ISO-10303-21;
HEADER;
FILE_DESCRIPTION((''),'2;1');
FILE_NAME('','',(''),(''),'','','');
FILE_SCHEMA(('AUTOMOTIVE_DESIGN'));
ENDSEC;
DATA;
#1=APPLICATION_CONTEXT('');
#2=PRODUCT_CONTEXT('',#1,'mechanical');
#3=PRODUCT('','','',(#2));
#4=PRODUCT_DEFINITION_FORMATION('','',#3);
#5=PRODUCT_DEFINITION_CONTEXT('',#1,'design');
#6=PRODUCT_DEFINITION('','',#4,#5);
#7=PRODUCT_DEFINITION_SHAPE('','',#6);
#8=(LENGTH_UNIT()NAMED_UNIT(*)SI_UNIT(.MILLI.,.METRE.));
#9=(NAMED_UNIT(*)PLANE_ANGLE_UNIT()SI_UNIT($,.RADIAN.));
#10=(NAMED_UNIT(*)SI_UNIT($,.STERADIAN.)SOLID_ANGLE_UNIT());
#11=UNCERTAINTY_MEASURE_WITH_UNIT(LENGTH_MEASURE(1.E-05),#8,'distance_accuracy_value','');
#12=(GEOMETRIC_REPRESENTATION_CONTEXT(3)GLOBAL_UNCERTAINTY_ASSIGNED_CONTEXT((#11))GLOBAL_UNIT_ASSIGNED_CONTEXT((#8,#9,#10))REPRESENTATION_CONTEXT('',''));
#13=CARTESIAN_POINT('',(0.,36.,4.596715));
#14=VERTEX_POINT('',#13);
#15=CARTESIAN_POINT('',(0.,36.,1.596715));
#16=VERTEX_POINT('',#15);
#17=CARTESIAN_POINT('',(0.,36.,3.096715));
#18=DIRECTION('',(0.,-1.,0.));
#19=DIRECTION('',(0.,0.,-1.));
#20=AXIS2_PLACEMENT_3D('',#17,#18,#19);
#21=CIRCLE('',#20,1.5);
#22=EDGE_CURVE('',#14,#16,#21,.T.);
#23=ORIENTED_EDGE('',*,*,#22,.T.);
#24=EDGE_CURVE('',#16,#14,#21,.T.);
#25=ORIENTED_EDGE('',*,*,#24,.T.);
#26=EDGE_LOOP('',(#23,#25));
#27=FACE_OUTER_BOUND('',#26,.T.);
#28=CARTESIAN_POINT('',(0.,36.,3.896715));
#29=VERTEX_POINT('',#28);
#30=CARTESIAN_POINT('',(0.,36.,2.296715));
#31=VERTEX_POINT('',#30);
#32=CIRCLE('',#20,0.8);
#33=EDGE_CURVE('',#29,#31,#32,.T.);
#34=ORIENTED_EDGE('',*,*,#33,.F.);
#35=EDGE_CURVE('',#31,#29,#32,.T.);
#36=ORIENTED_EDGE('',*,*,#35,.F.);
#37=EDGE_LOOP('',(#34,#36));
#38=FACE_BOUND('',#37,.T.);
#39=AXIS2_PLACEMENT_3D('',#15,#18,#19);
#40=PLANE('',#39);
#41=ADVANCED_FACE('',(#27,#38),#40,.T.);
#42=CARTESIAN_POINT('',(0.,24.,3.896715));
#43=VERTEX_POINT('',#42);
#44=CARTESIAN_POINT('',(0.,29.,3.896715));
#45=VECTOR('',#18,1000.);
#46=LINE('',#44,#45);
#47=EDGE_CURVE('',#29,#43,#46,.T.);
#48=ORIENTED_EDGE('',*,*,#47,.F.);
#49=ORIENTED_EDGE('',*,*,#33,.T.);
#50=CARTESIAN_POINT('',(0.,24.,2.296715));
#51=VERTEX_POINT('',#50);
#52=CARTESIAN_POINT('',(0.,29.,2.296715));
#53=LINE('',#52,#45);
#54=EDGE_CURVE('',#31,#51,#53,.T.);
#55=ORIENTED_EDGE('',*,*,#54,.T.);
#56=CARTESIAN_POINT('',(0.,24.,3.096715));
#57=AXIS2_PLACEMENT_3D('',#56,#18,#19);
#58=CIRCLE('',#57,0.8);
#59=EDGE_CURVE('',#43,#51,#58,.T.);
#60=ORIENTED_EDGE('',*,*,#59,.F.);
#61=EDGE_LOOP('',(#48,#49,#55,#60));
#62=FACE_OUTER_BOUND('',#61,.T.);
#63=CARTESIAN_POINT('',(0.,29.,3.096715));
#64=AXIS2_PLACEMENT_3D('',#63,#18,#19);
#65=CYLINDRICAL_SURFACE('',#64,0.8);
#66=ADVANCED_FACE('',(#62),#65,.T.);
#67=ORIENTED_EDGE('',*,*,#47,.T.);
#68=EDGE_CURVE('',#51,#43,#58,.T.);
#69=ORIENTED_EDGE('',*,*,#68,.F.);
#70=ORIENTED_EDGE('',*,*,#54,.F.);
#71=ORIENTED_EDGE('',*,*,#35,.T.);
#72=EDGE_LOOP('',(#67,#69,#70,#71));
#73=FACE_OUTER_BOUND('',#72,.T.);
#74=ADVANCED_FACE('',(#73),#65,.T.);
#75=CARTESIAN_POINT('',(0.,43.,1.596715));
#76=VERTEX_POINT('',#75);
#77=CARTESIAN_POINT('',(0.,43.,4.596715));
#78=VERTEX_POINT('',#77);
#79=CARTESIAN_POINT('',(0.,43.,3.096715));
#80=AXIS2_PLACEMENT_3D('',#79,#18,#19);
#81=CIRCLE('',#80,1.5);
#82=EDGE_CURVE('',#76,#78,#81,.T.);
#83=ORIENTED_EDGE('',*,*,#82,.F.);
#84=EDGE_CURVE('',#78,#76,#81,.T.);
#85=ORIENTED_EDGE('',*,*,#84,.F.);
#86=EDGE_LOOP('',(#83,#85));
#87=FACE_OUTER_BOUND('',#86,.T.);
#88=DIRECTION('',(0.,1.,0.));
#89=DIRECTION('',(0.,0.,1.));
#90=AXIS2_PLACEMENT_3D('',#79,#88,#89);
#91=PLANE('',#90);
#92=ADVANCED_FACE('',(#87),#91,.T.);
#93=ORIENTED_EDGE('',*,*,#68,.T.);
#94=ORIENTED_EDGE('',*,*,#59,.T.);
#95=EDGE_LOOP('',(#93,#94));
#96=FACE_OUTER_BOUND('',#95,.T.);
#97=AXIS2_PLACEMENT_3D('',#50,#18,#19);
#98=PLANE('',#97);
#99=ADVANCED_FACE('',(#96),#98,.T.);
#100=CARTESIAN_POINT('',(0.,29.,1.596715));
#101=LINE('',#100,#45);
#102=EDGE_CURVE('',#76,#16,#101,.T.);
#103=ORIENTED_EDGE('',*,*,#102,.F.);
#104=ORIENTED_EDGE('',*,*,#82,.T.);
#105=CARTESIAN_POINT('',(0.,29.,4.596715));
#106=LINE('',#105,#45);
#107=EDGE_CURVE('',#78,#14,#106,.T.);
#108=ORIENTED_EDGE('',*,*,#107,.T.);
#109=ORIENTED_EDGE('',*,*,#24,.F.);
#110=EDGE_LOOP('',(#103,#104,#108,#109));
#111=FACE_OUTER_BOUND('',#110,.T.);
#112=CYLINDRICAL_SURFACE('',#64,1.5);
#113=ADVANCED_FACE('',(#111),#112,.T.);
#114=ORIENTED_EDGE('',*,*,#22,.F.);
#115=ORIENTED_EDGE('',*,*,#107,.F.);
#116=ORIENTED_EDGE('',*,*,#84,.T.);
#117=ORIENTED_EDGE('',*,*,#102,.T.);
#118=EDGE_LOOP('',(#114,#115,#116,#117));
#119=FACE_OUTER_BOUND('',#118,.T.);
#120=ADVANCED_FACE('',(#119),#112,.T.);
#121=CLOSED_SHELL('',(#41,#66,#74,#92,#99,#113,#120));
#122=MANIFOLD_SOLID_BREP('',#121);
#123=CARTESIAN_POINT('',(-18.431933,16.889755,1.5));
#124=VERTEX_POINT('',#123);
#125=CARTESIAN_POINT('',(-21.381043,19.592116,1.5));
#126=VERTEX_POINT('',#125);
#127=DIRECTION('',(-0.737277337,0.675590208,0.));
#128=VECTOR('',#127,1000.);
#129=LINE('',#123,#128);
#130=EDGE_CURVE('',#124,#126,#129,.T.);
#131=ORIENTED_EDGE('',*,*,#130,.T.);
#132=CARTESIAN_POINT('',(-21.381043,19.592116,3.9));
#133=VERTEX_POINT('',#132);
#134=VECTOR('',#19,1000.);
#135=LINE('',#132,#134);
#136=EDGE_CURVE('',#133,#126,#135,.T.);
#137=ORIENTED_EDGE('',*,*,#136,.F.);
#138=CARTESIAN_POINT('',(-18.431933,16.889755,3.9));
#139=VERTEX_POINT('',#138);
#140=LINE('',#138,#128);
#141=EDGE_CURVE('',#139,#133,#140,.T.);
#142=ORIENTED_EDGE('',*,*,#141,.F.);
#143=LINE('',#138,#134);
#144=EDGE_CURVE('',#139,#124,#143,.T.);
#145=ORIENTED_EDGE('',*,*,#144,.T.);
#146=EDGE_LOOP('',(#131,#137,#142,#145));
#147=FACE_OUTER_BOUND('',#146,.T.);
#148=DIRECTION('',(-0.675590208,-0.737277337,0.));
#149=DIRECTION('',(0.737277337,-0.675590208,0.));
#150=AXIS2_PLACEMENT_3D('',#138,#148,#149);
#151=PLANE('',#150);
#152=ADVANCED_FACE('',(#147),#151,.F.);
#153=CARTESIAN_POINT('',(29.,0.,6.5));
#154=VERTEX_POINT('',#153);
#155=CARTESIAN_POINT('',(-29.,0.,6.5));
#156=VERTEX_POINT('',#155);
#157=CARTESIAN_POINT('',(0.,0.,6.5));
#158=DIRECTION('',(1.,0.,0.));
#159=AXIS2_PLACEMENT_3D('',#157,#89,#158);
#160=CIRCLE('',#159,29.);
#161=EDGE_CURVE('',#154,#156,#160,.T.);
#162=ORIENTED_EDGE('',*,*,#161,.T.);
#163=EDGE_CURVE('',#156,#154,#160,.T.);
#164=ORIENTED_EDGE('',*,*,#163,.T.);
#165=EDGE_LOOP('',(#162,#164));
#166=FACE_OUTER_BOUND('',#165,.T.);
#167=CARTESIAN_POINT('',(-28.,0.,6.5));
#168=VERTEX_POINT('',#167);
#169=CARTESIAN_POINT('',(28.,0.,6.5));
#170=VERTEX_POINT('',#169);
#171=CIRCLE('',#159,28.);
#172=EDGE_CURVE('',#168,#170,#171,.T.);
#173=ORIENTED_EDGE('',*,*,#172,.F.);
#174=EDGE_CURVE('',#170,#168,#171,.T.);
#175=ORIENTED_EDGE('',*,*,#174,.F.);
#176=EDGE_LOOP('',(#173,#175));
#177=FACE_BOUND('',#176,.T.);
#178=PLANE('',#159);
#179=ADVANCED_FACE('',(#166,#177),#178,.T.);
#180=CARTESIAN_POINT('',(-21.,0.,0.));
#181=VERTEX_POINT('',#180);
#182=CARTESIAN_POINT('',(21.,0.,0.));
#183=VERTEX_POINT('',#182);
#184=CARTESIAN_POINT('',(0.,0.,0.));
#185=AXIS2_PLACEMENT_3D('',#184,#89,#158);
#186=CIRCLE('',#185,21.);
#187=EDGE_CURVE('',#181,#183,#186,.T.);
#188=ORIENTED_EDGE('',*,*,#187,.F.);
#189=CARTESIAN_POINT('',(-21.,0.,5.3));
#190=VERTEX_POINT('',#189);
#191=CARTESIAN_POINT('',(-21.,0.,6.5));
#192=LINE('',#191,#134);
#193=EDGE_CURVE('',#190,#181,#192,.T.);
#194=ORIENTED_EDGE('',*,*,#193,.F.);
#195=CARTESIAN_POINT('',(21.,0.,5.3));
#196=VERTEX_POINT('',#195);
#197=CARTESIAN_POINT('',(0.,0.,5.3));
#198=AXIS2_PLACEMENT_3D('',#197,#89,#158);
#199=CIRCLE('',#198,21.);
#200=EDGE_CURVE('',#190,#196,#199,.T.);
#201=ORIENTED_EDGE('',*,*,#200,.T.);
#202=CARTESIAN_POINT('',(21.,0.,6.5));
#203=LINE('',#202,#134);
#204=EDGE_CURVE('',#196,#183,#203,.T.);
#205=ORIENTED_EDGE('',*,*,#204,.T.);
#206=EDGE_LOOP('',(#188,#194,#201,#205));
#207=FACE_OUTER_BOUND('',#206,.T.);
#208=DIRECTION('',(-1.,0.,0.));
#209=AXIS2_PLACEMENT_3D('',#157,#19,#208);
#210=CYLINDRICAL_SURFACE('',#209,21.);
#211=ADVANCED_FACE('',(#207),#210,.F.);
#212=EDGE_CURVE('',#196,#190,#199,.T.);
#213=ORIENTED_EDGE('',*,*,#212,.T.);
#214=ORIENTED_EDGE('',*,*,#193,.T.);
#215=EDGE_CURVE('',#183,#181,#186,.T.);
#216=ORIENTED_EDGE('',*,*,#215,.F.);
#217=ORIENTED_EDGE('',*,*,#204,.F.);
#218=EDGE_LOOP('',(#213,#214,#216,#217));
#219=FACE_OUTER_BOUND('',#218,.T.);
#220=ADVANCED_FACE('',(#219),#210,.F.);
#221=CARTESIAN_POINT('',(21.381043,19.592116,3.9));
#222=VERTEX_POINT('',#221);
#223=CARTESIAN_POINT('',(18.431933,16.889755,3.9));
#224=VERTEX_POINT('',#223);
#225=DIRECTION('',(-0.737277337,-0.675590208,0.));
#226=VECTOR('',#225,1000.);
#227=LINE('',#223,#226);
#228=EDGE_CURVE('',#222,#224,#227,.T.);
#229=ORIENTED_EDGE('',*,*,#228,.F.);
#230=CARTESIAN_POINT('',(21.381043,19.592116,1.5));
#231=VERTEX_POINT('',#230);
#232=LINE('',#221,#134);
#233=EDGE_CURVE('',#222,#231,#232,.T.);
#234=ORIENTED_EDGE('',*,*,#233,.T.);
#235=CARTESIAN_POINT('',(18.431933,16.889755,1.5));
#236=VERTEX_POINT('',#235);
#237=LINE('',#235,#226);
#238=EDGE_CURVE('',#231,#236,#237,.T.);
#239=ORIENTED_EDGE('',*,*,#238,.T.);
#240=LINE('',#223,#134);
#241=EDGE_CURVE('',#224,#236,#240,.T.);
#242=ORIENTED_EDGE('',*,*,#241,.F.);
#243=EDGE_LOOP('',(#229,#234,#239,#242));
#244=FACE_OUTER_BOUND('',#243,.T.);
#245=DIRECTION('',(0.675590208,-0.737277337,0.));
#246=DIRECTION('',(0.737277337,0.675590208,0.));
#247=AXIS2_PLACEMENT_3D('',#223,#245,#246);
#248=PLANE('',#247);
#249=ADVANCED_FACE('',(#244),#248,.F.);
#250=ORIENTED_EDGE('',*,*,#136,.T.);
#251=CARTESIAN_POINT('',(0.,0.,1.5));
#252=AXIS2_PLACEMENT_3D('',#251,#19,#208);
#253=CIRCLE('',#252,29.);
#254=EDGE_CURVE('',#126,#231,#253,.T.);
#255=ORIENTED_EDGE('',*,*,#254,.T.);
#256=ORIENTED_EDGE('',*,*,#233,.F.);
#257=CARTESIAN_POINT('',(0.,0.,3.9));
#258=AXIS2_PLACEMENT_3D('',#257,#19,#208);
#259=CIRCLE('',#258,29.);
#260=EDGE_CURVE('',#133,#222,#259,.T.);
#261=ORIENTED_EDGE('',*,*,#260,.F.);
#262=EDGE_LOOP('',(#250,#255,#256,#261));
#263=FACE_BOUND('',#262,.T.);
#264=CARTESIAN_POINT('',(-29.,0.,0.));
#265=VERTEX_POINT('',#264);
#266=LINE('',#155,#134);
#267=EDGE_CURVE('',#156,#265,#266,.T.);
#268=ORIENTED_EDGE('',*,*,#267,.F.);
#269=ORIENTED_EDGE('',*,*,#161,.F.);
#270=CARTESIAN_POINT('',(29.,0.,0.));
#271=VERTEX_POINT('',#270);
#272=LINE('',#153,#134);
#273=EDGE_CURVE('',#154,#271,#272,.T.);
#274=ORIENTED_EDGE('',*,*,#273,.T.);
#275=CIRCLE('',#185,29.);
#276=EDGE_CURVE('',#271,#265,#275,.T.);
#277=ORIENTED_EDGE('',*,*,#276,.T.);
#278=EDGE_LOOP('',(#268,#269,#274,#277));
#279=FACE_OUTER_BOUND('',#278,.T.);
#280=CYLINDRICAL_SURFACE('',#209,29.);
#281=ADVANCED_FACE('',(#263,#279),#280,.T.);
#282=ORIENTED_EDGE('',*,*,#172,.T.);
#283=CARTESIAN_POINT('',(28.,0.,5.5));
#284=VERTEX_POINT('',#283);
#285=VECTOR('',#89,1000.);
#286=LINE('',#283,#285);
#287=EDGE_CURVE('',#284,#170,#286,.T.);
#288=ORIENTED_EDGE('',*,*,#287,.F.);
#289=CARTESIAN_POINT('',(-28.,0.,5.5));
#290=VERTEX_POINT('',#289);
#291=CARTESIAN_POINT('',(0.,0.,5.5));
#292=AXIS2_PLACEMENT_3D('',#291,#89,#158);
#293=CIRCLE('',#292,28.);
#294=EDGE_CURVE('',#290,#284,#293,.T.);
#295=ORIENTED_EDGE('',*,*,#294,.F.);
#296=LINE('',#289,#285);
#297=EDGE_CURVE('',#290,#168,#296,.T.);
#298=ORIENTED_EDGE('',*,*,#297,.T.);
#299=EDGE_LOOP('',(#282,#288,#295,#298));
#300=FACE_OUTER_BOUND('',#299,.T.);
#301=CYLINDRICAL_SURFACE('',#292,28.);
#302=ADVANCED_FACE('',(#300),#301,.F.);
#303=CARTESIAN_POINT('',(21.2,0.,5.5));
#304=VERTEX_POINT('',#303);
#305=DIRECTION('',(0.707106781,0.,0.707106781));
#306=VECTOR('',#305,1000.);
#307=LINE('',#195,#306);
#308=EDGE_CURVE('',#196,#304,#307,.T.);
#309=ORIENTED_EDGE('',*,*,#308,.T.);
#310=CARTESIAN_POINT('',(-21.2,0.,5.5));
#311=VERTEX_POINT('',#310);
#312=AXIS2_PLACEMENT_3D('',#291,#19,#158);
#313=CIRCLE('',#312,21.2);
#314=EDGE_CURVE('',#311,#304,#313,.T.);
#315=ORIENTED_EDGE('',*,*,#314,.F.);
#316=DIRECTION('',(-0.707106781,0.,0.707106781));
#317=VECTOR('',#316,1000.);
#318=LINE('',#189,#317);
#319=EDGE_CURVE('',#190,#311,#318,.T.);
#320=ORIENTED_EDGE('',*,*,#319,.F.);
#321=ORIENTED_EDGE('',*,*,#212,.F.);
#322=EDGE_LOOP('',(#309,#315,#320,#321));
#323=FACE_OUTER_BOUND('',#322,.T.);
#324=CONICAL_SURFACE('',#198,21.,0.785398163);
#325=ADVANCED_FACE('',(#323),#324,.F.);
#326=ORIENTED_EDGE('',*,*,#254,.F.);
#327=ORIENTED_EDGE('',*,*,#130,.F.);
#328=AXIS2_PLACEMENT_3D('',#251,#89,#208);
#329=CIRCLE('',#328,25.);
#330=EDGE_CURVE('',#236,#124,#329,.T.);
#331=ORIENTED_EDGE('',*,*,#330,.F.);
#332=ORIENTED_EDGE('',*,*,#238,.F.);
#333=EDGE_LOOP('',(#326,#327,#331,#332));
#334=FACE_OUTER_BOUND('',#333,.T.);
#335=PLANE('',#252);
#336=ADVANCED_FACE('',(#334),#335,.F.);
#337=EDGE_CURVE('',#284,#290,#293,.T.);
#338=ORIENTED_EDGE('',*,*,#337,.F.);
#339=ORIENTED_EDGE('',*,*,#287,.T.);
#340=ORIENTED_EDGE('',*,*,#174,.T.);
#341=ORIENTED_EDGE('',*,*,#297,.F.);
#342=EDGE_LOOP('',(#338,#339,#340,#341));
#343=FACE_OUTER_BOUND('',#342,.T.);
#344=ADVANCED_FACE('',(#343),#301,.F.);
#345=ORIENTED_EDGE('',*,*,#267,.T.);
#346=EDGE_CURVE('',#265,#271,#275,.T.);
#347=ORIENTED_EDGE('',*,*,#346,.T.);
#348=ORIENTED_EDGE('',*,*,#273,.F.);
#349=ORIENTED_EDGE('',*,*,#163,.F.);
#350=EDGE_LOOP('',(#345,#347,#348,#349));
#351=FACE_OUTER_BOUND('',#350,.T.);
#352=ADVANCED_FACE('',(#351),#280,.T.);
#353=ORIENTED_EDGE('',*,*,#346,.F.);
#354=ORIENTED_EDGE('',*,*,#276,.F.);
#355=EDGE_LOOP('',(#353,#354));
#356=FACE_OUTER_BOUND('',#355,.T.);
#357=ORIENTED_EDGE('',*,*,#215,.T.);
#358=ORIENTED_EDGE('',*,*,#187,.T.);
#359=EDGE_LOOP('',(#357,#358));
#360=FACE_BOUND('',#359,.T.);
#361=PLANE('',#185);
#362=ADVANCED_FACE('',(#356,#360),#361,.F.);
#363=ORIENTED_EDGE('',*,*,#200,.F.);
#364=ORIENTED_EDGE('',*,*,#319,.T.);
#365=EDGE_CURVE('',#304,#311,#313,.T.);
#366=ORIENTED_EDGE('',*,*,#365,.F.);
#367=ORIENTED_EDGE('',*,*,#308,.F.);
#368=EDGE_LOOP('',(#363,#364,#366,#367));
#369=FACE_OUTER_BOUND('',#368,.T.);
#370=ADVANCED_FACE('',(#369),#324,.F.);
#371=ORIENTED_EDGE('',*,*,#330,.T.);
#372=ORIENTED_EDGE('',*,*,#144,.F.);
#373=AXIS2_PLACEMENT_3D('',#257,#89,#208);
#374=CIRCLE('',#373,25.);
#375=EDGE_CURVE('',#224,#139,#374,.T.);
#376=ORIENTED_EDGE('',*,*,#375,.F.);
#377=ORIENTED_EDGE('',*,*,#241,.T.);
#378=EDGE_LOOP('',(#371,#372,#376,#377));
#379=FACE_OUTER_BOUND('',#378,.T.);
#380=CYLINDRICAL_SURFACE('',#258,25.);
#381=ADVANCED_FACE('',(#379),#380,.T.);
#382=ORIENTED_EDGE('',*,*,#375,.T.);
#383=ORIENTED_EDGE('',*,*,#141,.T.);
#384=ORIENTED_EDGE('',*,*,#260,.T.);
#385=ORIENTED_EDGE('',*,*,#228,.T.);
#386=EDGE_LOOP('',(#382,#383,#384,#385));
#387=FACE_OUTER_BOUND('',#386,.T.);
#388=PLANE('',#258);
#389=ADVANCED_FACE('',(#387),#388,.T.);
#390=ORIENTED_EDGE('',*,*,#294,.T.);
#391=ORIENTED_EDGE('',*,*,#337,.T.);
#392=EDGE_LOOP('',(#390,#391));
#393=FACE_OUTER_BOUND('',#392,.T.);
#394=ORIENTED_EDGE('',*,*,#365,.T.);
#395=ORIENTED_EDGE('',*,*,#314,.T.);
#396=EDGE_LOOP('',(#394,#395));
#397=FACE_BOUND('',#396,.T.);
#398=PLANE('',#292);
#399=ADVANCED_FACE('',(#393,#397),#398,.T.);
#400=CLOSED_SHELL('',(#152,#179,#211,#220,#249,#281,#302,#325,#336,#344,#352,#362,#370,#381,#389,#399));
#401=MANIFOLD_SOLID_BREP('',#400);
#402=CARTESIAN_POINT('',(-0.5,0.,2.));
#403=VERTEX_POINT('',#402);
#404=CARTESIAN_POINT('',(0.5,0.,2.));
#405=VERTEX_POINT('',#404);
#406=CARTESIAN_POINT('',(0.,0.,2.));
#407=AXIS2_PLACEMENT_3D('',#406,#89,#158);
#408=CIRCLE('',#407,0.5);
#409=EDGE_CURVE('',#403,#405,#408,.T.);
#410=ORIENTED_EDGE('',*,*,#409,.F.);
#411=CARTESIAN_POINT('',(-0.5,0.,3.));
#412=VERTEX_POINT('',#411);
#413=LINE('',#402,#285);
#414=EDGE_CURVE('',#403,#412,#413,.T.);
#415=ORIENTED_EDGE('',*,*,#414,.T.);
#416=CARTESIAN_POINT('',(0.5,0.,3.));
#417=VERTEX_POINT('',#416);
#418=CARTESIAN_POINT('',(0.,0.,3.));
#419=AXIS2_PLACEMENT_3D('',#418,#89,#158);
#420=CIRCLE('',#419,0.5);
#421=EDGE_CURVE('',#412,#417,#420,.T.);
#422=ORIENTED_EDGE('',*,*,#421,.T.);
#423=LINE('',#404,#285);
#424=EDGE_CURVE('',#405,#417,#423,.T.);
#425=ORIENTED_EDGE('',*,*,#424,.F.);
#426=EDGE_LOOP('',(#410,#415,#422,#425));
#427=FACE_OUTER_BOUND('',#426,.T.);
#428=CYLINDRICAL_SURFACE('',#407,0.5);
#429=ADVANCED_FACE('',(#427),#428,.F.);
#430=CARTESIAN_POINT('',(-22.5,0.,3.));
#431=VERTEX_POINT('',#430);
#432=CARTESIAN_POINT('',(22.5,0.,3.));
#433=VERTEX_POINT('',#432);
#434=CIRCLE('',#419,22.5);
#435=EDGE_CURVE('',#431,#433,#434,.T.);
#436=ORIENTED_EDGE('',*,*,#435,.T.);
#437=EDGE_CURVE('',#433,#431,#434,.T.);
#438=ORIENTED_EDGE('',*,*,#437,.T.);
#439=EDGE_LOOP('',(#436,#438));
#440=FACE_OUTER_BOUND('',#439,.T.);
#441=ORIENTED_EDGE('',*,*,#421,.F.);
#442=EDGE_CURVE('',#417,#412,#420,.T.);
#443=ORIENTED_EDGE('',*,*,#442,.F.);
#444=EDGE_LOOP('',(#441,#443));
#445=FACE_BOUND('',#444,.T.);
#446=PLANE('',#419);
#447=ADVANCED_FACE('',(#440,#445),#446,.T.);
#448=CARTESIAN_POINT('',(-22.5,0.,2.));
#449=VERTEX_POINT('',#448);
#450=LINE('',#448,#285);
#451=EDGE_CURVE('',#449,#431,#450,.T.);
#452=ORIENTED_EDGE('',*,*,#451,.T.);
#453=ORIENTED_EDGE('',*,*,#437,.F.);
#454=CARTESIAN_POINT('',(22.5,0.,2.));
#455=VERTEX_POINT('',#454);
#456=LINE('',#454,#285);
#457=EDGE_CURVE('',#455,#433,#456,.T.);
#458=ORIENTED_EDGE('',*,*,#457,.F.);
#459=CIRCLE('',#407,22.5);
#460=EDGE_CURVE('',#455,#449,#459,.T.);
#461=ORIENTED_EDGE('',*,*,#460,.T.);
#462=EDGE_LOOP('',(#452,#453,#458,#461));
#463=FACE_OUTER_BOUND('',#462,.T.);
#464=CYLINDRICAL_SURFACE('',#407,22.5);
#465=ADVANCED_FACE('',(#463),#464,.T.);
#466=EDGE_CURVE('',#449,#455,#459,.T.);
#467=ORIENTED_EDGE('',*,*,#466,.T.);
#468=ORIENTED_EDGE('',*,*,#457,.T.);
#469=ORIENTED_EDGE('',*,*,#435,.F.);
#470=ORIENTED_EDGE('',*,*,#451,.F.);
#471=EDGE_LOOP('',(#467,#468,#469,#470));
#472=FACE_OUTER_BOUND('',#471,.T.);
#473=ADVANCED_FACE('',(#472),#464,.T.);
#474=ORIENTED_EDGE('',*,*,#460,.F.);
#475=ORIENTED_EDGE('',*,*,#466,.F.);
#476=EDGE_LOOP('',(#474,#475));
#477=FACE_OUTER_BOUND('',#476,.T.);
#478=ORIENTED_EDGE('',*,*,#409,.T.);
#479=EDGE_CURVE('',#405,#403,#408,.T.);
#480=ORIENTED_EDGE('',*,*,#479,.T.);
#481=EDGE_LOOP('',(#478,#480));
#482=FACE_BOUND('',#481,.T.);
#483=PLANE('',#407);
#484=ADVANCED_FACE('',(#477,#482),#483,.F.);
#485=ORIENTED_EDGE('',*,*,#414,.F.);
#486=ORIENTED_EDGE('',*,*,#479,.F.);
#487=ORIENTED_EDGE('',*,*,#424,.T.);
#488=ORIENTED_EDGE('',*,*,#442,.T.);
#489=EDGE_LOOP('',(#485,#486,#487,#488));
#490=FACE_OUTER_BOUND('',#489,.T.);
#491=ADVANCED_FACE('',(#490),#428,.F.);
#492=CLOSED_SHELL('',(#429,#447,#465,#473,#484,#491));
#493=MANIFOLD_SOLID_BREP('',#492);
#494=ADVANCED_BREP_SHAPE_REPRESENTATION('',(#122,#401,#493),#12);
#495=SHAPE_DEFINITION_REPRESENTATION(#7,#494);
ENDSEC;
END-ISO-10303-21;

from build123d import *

# Parameters (mm, degrees)
SKETCH_1_R          = 29
SKETCH_1_R_2        = 21
EXTRUDE_1_DEPTH     = 6.5
SKETCH_7_R          = 28
CUT_EXTRUDE_5_DEPTH = 1
CUT_EXTRUDE_START   = -1.5
CUT_EXTRUDE_6_DEPTH = 2.4
MOVE_FACE_1_BY      = 5
EXTRUDE_START       = -3.5
SKETCH_11_R         = 22.5
SKETCH_11_R_2       = 0.5
EXTRUDE_2_DEPTH     = 1
CHAMFER_1_SIZE      = 0.2


with BuildPart() as part:
    # 草图1 → 凸台-拉伸1 (new body)
    with BuildSketch(Plane.XY):
        with Locations(Location((0, 0, 0), (0, 0, 180))):
            Circle(SKETCH_1_R)
        with Locations(Location((0, 0, 0), (0, 0, 180))):
            Circle(SKETCH_1_R_2, mode=Mode.SUBTRACT)
    extrude(amount=EXTRUDE_1_DEPTH)

    # 草图7 → 切除-拉伸5 (cut)
    with BuildSketch(Plane.XY.offset(6.5)):
        Circle(SKETCH_7_R)
    extrude(amount=-CUT_EXTRUDE_5_DEPTH, mode=Mode.SUBTRACT)

    # 草图9 → 切除-拉伸6 (cut)
    with BuildSketch(Plane(origin=(0, 0, 0), x_dir=(-1, 0, 0), z_dir=(0, 0, -1)).offset(CUT_EXTRUDE_START)):
        with BuildLine():
            Line((-18.43193342, 16.88975519), (-21.381042767, 19.592116021))
            ThreePointArc((-21.381042767, 19.592116021), (0, 29), (21.381042767, 19.592116021))
            Line((21.381042767, 19.592116021), (18.43193342, 16.88975519))
            ThreePointArc((18.43193342, 16.88975519), (0, 25), (-18.43193342, 16.88975519))
        make_face()
    extrude(amount=-CUT_EXTRUDE_6_DEPTH, mode=Mode.SUBTRACT)

    # 倒角1
    chamfer_1_edges = [part.edges().sort_by_distance(p)[0] for p in [
        (21, 0, 5.5),
    ]]
    chamfer(chamfer_1_edges, length=CHAMFER_1_SIZE)


with BuildPart() as body_2:
    # 草图10 → 旋转4 (revolve)
    with BuildSketch(Plane(origin=(0, 0, 0), x_dir=(0, 0, -1), z_dir=(1, 0, 0))):
        Polygon((-3.096715261, 43), (-1.596715261, 43), (-1.596715261, 36), (-2.296715261, 36), (-2.296715261, 29), (-3.096715261, 29), align=None)
    revolve(axis=Axis((0, 29, 3.096715261), (0, 1, 0)))

    # Move Face 1: a face moved outward by 5.0
    extrude(body_2.faces().sort_by_distance((0, 29, 3.096715261))[0], amount=MOVE_FACE_1_BY, dir=(0, -1, 0))


with BuildPart() as body_3:
    # 草图11 → 凸台-拉伸2 (new body)
    with BuildSketch(Plane.XY.offset(6.5).offset(EXTRUDE_START)):
        Circle(SKETCH_11_R)
        Circle(SKETCH_11_R_2, mode=Mode.SUBTRACT)
    extrude(amount=-EXTRUDE_2_DEPTH)


solid = Compound([part.part, body_2.part, body_3.part])
